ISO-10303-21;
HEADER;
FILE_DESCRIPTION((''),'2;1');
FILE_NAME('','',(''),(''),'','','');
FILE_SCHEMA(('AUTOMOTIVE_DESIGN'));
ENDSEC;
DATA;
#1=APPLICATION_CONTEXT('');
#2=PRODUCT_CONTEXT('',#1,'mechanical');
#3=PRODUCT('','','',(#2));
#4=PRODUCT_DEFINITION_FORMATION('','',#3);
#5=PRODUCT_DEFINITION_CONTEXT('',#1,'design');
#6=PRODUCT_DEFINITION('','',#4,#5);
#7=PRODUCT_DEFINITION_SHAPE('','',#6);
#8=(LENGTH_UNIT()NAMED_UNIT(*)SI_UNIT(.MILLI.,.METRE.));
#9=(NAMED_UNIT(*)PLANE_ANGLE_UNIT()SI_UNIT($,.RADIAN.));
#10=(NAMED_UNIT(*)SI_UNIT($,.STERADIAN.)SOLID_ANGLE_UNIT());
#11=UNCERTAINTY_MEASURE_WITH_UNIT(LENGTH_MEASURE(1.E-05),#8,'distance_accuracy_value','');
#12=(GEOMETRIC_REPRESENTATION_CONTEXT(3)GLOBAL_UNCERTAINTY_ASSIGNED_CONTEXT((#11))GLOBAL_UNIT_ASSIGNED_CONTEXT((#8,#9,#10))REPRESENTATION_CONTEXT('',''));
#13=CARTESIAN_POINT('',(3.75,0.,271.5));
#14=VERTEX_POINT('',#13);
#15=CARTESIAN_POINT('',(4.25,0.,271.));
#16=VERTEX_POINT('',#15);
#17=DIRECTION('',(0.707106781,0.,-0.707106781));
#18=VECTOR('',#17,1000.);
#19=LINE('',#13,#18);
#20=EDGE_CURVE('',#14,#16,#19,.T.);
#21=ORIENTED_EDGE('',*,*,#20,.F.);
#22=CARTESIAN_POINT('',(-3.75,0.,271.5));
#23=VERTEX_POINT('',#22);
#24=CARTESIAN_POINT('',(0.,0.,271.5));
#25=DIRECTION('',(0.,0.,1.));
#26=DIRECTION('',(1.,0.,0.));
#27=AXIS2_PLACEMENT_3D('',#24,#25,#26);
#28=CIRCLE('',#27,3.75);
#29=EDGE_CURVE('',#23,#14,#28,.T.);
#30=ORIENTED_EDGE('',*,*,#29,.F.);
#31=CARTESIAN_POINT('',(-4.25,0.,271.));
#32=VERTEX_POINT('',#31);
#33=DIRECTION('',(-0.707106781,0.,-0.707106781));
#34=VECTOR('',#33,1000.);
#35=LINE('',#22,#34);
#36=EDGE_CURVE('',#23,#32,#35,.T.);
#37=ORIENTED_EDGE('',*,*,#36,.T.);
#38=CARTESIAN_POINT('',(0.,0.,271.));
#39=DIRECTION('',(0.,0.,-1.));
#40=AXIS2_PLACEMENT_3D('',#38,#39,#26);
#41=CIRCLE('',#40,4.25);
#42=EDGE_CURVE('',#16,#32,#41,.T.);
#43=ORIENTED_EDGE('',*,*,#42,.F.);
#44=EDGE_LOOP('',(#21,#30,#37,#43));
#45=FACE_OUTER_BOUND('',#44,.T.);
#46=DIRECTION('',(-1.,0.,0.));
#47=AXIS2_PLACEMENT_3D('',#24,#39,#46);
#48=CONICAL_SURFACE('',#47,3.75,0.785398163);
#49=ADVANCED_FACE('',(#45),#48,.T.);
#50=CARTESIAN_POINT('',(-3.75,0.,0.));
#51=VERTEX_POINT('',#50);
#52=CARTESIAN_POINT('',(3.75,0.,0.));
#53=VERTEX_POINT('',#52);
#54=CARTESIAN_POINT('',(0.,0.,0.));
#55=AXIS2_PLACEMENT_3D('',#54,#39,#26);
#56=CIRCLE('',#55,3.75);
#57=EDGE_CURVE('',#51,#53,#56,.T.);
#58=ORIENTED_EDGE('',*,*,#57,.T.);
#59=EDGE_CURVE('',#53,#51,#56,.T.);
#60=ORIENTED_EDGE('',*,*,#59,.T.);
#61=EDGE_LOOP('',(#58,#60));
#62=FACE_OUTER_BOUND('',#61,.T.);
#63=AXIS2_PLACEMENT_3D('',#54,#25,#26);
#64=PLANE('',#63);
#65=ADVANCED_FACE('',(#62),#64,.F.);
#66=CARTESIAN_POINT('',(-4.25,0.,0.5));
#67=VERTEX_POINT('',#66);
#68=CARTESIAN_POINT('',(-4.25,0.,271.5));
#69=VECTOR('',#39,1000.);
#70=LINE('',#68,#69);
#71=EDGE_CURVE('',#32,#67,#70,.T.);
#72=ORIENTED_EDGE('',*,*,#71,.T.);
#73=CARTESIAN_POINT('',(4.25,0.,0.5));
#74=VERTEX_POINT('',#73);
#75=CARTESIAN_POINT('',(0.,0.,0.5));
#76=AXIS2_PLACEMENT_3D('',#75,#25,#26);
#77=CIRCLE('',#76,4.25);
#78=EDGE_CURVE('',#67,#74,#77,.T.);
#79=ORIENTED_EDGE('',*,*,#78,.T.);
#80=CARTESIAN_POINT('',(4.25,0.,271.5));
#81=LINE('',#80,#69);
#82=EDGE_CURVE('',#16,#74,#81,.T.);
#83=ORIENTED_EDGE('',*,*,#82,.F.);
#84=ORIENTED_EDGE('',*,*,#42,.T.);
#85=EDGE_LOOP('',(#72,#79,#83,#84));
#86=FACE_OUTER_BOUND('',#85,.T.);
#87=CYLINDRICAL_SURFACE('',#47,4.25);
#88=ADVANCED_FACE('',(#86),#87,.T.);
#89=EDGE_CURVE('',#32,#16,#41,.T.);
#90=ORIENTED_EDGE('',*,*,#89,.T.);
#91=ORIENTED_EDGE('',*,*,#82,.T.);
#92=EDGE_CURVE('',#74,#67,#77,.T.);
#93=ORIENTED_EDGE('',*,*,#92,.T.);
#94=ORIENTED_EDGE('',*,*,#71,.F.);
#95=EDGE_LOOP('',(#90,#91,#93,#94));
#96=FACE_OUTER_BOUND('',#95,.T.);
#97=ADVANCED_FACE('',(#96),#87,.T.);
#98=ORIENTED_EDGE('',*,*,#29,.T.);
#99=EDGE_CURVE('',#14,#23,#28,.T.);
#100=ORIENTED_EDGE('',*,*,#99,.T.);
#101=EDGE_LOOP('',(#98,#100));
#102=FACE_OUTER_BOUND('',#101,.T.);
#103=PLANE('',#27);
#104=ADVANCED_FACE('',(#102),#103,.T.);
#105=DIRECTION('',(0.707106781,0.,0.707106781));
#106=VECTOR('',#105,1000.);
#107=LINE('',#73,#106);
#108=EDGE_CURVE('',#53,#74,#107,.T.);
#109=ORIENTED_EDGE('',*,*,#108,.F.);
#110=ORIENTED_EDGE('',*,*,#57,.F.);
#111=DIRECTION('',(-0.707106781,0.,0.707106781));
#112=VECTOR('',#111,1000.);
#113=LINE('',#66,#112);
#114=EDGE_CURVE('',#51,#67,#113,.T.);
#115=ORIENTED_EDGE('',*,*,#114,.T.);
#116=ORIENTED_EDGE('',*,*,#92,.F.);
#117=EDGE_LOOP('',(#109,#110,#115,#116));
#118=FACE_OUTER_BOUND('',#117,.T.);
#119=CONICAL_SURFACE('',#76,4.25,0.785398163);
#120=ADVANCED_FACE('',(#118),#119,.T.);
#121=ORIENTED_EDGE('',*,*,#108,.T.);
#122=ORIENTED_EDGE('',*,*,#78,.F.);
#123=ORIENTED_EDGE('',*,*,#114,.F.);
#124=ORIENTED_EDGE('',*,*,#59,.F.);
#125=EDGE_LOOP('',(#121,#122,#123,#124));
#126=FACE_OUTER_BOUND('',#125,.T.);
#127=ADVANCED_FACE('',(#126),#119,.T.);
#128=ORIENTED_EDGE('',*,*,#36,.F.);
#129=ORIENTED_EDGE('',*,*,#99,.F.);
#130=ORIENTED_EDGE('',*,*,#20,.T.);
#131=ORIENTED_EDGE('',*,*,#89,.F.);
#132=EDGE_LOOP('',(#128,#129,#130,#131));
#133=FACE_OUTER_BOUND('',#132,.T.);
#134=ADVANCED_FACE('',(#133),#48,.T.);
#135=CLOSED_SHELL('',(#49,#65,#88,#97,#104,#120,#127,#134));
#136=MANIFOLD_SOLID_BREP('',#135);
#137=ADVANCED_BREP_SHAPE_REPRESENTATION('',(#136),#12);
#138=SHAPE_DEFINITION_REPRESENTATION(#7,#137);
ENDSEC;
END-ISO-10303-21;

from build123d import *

# Parameters (mm, degrees)
SKETCH1_R           = 4.25
BOSS_EXTRUDE1_DEPTH = 271.5
CHAMFER1_SIZE       = 0.5


with BuildPart() as part:
    # Sketch1 → Boss-Extrude1 (new body)
    with BuildSketch(Plane.XY):
        Circle(SKETCH1_R)
    extrude(amount=BOSS_EXTRUDE1_DEPTH)

    # Chamfer1
    chamfer1_edges = [part.edges().sort_by_distance(p)[0] for p in [
        (-4.25, 0, 0),
        (-4.25, 0, 271.5),
    ]]
    chamfer(chamfer1_edges, length=CHAMFER1_SIZE)


solid = part.part
